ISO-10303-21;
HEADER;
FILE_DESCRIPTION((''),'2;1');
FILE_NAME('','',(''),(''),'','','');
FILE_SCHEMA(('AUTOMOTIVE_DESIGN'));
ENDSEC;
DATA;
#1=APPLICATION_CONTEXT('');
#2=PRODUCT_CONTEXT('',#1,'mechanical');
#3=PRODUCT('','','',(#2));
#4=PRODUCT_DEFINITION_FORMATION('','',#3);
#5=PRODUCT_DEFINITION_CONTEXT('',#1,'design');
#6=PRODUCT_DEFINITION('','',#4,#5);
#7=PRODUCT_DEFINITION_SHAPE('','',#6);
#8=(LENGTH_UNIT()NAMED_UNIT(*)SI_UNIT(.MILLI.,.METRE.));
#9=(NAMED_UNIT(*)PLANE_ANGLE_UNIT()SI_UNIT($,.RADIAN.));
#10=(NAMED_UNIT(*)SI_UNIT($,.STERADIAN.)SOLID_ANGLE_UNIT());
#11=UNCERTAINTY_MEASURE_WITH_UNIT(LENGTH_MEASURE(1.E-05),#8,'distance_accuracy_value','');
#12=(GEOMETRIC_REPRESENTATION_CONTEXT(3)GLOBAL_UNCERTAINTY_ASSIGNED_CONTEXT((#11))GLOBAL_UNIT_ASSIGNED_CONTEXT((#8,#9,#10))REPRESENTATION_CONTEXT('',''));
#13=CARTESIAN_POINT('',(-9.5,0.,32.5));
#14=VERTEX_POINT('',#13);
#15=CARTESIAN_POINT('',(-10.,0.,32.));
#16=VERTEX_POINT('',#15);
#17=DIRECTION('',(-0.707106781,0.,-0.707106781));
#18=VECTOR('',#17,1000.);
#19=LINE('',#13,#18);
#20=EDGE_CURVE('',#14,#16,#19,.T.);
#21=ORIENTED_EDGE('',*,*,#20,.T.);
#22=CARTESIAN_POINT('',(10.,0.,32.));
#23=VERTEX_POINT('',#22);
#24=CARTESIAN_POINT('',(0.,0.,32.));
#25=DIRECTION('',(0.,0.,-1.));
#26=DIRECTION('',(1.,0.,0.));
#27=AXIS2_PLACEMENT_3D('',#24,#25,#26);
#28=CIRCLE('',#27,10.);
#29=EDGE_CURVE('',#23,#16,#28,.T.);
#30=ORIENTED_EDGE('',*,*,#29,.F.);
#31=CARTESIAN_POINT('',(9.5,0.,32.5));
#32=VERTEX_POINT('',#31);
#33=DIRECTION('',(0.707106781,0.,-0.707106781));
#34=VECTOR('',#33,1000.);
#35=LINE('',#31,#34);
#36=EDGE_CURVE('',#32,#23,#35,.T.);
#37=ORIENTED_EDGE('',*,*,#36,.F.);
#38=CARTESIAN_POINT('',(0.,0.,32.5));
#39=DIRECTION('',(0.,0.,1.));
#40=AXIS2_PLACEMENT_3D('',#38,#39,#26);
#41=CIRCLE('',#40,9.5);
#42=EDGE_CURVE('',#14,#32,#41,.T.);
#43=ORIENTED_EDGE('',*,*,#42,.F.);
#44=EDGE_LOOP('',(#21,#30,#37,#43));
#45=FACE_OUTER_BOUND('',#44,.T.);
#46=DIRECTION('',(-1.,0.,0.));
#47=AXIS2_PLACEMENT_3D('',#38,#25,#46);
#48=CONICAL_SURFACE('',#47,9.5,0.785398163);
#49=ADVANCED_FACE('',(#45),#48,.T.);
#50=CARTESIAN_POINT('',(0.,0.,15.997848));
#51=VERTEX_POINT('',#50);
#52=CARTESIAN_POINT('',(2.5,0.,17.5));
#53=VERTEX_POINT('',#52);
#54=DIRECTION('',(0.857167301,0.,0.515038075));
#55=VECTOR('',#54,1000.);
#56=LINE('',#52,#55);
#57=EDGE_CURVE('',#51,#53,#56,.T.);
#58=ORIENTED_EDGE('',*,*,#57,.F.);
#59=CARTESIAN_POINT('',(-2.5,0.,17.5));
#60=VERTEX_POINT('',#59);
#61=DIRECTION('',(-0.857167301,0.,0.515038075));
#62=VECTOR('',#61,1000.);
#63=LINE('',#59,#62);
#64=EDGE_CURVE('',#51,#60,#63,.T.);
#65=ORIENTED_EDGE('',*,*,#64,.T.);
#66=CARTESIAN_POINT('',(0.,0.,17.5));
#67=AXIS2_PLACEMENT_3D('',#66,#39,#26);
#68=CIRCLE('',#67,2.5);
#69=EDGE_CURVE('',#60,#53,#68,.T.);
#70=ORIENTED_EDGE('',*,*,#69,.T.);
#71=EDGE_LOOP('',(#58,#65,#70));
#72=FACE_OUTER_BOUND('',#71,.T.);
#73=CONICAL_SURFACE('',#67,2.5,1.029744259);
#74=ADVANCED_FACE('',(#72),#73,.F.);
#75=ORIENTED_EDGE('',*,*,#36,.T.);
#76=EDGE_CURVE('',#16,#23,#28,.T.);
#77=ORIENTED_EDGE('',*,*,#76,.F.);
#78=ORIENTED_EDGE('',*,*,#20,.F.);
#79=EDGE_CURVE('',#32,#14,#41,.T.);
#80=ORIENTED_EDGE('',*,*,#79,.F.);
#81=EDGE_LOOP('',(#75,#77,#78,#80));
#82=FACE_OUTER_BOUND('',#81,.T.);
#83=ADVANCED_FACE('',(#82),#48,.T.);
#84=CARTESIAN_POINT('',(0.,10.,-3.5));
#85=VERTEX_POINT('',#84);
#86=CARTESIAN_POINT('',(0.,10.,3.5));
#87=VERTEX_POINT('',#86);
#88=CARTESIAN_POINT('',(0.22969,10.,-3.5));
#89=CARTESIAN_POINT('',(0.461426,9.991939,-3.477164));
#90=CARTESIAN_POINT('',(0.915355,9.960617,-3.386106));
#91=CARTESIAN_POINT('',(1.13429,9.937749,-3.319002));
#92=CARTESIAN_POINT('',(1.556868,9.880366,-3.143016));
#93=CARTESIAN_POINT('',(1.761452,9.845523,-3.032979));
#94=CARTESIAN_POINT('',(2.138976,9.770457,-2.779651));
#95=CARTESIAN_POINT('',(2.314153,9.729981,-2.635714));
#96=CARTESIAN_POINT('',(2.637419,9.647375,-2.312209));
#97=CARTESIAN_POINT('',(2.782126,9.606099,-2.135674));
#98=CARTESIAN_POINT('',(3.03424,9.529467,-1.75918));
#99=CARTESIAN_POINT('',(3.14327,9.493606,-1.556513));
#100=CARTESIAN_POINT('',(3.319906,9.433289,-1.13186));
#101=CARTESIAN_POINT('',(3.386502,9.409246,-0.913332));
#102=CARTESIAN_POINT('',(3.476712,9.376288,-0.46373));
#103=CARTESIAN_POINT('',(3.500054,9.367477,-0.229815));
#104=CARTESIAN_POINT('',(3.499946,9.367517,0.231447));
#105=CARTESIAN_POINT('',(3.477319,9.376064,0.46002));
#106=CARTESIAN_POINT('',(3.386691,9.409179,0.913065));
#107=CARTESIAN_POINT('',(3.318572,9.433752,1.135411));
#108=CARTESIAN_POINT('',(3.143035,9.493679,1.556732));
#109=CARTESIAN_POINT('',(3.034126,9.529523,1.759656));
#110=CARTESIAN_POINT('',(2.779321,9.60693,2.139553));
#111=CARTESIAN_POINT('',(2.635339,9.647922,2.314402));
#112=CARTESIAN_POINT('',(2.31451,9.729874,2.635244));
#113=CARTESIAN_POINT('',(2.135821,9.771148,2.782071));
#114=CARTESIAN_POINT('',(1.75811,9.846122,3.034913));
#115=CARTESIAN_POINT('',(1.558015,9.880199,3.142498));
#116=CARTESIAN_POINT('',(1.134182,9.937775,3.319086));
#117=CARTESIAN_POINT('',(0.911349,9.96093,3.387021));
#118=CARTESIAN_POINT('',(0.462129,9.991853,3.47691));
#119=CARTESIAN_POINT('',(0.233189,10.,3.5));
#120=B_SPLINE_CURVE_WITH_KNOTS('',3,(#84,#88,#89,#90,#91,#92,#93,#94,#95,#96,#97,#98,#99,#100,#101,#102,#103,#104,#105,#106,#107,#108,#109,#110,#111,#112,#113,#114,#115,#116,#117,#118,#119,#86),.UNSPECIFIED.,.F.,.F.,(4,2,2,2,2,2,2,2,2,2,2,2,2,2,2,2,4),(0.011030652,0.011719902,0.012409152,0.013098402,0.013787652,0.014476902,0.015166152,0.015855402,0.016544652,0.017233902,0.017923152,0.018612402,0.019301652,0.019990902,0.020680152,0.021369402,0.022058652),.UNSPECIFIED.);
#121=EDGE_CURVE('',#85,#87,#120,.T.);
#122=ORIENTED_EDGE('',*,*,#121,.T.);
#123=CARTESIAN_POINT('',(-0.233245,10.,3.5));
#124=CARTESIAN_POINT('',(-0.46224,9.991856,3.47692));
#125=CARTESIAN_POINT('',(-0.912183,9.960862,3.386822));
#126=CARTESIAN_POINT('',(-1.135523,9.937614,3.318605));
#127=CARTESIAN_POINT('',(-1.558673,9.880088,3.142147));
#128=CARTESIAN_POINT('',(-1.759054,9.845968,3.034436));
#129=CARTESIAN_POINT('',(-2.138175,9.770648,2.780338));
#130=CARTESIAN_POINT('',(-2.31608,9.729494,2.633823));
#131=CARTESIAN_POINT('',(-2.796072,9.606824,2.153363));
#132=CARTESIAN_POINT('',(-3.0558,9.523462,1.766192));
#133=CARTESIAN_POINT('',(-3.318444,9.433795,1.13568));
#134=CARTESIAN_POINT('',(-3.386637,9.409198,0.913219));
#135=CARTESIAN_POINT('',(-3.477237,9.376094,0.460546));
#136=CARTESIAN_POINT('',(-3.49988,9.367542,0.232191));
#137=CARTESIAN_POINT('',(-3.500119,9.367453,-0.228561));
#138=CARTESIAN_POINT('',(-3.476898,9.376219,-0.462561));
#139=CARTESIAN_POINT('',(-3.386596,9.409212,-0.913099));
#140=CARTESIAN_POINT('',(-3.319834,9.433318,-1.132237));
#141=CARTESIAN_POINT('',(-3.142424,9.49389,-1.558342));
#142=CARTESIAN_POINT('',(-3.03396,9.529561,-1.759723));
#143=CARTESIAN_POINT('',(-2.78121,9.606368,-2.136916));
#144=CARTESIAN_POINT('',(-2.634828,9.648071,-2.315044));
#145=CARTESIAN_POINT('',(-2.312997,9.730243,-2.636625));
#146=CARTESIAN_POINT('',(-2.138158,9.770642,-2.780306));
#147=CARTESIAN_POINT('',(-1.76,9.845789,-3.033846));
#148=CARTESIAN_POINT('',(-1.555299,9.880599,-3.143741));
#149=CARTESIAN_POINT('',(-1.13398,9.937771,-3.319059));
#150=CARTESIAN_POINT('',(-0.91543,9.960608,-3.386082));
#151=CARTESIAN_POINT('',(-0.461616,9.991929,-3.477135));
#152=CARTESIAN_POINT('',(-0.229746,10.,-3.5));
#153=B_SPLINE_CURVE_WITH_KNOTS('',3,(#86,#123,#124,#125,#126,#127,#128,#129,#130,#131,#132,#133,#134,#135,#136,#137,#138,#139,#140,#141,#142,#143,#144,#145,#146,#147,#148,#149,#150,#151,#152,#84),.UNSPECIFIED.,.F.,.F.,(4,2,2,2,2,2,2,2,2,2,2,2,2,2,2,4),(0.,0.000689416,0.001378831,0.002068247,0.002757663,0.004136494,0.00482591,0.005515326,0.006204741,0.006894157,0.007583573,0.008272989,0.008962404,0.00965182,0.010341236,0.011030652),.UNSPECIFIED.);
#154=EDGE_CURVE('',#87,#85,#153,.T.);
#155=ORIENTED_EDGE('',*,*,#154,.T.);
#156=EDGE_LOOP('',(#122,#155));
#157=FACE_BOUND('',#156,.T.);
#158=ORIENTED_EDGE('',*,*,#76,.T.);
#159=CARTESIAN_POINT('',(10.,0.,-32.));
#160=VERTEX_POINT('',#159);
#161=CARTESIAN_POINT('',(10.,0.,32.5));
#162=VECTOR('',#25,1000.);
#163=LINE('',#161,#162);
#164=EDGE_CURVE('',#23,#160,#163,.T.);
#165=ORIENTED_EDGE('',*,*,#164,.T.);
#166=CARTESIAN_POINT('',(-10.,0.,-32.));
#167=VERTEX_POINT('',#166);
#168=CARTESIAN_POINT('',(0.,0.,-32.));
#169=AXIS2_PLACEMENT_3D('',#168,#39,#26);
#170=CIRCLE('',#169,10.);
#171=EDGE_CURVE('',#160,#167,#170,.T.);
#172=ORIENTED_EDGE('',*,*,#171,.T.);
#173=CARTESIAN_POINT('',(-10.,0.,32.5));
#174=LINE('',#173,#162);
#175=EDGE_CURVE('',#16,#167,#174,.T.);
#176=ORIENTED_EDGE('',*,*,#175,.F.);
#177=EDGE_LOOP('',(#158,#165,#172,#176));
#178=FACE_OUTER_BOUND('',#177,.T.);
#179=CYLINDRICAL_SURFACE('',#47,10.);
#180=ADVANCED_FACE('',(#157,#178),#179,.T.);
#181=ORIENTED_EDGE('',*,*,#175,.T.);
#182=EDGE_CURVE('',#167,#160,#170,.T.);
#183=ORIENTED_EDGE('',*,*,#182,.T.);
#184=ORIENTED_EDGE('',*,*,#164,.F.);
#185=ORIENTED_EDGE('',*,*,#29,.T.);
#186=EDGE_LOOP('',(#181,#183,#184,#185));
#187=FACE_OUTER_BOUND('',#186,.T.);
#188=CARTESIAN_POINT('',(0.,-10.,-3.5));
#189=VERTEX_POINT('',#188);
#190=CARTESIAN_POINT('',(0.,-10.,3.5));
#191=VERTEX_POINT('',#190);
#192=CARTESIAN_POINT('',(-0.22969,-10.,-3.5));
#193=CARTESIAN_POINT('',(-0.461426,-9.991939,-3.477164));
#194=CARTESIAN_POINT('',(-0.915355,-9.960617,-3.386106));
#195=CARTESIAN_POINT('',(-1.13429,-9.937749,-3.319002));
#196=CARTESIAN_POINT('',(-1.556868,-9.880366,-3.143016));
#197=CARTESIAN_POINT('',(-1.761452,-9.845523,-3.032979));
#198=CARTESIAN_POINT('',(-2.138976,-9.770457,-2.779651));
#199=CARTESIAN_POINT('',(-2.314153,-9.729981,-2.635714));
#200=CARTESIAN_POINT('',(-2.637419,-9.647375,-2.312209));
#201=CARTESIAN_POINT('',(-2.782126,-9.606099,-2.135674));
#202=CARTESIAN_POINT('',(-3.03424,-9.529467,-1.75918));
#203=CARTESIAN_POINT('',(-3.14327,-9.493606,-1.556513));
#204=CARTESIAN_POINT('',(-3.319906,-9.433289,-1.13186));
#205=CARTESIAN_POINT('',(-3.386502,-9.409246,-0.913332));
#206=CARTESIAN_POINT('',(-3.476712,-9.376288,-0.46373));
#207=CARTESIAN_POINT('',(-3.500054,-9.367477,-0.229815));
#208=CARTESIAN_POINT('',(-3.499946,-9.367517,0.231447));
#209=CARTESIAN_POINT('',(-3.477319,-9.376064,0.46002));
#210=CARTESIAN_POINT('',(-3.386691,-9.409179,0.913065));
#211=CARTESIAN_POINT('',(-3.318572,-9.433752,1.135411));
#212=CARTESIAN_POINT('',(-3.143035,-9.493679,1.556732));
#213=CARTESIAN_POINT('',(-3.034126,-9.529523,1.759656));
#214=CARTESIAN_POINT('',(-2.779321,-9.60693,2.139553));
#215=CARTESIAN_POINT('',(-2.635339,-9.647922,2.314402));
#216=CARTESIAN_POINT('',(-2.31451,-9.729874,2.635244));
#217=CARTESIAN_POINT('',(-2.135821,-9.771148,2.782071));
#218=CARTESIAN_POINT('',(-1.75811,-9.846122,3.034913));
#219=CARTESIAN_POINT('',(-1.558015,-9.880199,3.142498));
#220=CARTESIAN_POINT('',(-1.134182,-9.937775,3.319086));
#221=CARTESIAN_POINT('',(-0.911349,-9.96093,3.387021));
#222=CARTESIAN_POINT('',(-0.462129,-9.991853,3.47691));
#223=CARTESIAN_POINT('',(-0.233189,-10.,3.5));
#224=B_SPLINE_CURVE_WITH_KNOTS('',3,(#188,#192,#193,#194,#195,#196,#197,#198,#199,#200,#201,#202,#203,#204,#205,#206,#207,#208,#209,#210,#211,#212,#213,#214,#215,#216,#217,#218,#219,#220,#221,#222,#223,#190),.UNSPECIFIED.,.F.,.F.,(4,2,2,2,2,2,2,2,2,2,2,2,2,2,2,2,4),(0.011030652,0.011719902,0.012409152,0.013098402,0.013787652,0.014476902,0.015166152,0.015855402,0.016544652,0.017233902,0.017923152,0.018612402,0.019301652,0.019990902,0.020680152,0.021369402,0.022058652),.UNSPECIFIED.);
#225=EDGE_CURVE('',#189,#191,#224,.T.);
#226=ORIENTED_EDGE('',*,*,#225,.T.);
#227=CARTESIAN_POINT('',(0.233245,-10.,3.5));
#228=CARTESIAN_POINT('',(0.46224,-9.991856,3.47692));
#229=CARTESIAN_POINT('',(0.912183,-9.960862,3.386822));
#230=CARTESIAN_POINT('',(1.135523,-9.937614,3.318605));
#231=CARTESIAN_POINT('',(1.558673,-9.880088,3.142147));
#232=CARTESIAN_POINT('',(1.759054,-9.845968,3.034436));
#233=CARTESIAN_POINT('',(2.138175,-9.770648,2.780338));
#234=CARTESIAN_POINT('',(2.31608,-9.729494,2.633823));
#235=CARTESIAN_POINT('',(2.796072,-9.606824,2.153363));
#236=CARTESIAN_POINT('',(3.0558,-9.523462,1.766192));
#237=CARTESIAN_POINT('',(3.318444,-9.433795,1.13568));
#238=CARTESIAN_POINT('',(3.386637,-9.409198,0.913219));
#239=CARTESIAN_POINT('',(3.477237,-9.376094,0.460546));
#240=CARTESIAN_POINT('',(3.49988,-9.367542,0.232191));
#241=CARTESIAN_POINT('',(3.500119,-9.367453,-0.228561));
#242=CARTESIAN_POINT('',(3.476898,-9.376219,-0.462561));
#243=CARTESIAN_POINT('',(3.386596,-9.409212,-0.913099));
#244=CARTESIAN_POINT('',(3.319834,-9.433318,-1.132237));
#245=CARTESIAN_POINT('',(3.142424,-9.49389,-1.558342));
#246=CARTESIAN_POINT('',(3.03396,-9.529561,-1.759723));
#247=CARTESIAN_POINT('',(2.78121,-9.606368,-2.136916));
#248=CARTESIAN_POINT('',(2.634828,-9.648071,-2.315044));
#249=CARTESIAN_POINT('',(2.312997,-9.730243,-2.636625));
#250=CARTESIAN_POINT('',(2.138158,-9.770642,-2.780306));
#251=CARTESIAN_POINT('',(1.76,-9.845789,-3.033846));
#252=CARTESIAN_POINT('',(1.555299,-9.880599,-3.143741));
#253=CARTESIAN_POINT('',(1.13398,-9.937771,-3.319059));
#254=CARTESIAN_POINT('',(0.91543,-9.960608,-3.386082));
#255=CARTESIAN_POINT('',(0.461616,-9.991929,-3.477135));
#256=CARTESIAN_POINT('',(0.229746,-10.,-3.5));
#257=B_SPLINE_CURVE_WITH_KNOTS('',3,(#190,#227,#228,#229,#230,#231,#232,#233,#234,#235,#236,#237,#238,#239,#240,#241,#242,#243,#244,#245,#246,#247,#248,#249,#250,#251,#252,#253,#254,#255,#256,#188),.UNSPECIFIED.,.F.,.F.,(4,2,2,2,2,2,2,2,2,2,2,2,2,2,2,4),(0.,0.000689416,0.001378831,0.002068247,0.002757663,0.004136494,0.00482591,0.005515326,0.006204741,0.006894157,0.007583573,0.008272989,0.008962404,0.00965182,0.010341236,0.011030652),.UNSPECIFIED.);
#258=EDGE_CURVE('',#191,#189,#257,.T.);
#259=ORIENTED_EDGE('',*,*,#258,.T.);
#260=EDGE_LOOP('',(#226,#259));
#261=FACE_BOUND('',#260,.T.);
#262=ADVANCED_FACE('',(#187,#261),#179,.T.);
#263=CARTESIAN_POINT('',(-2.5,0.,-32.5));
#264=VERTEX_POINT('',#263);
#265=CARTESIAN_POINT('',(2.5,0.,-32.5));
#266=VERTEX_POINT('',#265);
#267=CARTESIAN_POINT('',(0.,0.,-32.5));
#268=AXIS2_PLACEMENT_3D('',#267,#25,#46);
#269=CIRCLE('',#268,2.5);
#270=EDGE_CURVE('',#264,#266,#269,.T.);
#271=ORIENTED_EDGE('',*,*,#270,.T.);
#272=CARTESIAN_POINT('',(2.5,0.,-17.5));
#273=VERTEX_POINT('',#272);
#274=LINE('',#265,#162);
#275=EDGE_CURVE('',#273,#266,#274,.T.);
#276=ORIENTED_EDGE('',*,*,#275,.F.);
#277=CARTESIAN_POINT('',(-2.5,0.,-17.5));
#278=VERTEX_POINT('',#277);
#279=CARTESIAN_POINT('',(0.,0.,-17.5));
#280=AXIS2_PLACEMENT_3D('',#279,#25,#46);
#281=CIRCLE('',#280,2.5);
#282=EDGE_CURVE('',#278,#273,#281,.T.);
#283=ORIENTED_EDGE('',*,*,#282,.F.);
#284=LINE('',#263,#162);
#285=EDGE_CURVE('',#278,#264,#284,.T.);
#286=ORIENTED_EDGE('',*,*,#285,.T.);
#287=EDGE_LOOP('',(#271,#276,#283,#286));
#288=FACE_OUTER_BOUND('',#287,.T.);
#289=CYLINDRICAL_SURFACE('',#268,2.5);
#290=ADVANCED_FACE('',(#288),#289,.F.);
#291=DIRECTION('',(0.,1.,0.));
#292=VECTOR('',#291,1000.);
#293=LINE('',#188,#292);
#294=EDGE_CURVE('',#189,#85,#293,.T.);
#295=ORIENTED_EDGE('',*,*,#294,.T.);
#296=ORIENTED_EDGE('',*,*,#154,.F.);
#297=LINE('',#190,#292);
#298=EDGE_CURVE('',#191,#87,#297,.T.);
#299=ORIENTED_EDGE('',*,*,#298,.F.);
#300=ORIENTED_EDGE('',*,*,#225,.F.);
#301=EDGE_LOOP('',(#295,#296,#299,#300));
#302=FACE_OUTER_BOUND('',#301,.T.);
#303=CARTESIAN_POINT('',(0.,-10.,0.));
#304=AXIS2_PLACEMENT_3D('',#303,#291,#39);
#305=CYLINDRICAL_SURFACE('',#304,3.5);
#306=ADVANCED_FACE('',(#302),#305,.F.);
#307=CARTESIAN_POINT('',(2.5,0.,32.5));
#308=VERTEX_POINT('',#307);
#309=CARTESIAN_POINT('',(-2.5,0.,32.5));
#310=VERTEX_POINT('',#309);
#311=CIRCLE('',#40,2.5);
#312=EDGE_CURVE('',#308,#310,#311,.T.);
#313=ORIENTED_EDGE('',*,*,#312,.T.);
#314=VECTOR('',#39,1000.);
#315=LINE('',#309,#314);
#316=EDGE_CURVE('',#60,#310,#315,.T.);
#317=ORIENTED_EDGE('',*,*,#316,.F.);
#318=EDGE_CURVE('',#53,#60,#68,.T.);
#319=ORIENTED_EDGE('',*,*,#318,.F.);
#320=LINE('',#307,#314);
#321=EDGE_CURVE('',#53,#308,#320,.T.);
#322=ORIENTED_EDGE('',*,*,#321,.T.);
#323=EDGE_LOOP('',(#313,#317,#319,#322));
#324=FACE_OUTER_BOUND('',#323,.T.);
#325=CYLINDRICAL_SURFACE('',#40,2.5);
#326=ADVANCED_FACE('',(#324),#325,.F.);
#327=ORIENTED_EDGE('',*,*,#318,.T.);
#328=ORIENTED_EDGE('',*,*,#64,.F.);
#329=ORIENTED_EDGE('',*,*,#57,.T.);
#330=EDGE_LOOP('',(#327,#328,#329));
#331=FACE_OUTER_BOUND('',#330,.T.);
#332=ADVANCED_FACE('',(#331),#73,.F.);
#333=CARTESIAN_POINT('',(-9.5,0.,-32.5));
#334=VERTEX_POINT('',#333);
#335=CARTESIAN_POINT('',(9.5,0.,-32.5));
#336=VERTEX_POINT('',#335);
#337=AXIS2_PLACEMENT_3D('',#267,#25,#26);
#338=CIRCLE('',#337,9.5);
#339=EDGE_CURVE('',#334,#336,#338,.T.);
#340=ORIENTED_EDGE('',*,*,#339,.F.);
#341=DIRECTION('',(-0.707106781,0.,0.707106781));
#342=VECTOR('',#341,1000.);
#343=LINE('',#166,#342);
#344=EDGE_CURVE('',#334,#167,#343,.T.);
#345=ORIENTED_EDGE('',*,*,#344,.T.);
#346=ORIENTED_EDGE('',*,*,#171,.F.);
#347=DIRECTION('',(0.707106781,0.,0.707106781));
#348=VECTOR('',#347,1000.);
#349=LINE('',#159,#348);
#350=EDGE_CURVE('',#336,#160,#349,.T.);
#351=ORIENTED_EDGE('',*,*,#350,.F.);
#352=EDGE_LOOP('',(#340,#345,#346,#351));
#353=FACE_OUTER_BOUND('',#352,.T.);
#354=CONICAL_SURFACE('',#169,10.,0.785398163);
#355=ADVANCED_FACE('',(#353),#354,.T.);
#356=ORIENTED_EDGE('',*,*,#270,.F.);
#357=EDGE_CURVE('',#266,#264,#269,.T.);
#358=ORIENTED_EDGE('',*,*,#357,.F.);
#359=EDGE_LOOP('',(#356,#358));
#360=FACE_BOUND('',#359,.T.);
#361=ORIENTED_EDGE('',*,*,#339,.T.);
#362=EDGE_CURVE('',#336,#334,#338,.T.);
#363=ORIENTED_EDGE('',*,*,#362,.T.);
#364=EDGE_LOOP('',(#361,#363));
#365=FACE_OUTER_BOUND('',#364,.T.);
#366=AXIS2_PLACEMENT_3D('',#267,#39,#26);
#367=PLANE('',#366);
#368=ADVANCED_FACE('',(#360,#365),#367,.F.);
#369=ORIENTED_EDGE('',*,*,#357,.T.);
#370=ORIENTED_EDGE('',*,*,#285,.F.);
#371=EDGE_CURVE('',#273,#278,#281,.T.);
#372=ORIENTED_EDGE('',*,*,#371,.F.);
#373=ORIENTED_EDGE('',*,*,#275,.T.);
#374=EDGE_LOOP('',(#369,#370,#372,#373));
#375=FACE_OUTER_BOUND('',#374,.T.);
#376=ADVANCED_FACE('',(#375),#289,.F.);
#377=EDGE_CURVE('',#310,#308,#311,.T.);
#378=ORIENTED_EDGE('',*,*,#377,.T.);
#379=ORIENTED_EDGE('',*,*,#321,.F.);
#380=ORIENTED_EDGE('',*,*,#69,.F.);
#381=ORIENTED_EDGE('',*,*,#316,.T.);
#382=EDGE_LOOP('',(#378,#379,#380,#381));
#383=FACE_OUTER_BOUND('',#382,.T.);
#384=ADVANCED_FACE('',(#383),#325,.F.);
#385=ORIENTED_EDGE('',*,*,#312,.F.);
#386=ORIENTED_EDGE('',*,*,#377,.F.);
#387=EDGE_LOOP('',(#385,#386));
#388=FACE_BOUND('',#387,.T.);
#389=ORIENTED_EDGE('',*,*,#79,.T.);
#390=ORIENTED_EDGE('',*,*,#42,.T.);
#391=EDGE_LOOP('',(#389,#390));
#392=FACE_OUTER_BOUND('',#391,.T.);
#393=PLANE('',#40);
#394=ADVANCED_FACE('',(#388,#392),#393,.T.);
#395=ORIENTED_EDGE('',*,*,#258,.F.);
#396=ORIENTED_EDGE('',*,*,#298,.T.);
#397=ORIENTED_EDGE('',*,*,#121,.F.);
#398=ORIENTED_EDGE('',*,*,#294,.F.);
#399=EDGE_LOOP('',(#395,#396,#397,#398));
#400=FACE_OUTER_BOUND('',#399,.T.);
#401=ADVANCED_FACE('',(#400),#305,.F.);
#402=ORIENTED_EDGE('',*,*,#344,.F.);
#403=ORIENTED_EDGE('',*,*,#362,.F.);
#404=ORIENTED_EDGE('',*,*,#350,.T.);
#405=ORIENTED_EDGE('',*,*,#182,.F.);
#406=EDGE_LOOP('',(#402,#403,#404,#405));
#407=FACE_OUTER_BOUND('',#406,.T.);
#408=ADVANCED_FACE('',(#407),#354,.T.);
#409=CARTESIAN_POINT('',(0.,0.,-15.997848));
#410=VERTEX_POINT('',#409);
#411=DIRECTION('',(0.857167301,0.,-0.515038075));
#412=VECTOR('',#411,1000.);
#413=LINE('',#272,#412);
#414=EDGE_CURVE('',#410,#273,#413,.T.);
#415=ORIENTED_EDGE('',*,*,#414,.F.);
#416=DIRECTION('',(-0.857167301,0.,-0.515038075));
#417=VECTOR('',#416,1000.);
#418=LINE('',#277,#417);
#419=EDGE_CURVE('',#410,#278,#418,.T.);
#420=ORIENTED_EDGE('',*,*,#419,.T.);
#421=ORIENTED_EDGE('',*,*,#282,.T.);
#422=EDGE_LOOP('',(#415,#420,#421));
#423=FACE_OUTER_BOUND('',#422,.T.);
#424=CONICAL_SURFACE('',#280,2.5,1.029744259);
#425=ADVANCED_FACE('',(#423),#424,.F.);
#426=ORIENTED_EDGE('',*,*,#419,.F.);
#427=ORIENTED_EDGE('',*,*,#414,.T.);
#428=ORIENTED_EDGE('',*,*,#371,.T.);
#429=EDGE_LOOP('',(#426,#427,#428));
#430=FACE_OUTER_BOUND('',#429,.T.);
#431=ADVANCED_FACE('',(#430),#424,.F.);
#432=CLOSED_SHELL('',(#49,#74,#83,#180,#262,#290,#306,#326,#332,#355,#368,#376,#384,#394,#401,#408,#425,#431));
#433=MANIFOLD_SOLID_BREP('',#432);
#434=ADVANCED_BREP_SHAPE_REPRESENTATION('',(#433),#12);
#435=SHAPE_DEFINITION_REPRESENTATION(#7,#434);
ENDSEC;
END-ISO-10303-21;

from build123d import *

# Parameters (mm, degrees)
SKETCH1_R               = 10
BOSS_EXTRUDE1_DEPTH     = 32.5
CHAMFER1_SIZE           = 0.5
M6_TAPPED_HOLE1_D       = 5
M6_TAPPED_HOLE1_DEPTH   = 15
M6_TAPPED_HOLE1_TIP     = 1.502151548
M6_TAPPED_HOLE2_D       = 5
M6_TAPPED_HOLE2_DEPTH   = 15
M6_TAPPED_HOLE2_TIP     = 1.502151548
CUT_EXTRUDE1_DEPTH      = 36.443617197
CUT_EXTRUDE1_DEPTH_BACK = 36.443617197
SKETCH8_R               = 3.5


with BuildPart() as part:
    # Sketch1 → Boss-Extrude1 (new, symmetric)
    with BuildSketch(Plane.XY):
        Circle(SKETCH1_R)
    extrude(amount=BOSS_EXTRUDE1_DEPTH, both=True)

    # Chamfer1
    chamfer1_edges = [part.edges().sort_by_distance(p)[0] for p in [
        (-10, 0, -32.5),
        (-10, 0, 32.5),
    ]]
    chamfer(chamfer1_edges, length=CHAMFER1_SIZE)

    # M6 Tapped Hole1
    with Locations(Plane.XY.offset(32.5)):
        with Locations((0, 0)):
            Hole(M6_TAPPED_HOLE1_D / 2, depth=M6_TAPPED_HOLE1_DEPTH)
            with Locations((0, 0, -(M6_TAPPED_HOLE1_DEPTH + M6_TAPPED_HOLE1_TIP / 2))):  # 118° drill point
                Cone(0, M6_TAPPED_HOLE1_D / 2, M6_TAPPED_HOLE1_TIP, mode=Mode.SUBTRACT)

    # M6 Tapped Hole2
    with Locations(Plane(origin=(0, 0, -32.5), x_dir=(-1, 0, 0), z_dir=(0, 0, -1))):
        with Locations((0, 0)):
            Hole(M6_TAPPED_HOLE2_D / 2, depth=M6_TAPPED_HOLE2_DEPTH)
            with Locations((0, 0, -(M6_TAPPED_HOLE2_DEPTH + M6_TAPPED_HOLE2_TIP / 2))):  # 118° drill point
                Cone(0, M6_TAPPED_HOLE2_D / 2, M6_TAPPED_HOLE2_TIP, mode=Mode.SUBTRACT)

    # Sketch8 → Cut-Extrude1 (cut, two sides: drawn at the far end of the back side and taken through both)
    with BuildSketch(Plane(origin=(0, 0, 0), x_dir=(1, 0, 0), z_dir=(0, 1, 0)).offset(-CUT_EXTRUDE1_DEPTH_BACK)):
        with Locations(Location((0, 0, 0), (0, 0, 270))):
            Circle(SKETCH8_R)
    extrude(amount=CUT_EXTRUDE1_DEPTH + CUT_EXTRUDE1_DEPTH_BACK, mode=Mode.SUBTRACT)


solid = part.part
